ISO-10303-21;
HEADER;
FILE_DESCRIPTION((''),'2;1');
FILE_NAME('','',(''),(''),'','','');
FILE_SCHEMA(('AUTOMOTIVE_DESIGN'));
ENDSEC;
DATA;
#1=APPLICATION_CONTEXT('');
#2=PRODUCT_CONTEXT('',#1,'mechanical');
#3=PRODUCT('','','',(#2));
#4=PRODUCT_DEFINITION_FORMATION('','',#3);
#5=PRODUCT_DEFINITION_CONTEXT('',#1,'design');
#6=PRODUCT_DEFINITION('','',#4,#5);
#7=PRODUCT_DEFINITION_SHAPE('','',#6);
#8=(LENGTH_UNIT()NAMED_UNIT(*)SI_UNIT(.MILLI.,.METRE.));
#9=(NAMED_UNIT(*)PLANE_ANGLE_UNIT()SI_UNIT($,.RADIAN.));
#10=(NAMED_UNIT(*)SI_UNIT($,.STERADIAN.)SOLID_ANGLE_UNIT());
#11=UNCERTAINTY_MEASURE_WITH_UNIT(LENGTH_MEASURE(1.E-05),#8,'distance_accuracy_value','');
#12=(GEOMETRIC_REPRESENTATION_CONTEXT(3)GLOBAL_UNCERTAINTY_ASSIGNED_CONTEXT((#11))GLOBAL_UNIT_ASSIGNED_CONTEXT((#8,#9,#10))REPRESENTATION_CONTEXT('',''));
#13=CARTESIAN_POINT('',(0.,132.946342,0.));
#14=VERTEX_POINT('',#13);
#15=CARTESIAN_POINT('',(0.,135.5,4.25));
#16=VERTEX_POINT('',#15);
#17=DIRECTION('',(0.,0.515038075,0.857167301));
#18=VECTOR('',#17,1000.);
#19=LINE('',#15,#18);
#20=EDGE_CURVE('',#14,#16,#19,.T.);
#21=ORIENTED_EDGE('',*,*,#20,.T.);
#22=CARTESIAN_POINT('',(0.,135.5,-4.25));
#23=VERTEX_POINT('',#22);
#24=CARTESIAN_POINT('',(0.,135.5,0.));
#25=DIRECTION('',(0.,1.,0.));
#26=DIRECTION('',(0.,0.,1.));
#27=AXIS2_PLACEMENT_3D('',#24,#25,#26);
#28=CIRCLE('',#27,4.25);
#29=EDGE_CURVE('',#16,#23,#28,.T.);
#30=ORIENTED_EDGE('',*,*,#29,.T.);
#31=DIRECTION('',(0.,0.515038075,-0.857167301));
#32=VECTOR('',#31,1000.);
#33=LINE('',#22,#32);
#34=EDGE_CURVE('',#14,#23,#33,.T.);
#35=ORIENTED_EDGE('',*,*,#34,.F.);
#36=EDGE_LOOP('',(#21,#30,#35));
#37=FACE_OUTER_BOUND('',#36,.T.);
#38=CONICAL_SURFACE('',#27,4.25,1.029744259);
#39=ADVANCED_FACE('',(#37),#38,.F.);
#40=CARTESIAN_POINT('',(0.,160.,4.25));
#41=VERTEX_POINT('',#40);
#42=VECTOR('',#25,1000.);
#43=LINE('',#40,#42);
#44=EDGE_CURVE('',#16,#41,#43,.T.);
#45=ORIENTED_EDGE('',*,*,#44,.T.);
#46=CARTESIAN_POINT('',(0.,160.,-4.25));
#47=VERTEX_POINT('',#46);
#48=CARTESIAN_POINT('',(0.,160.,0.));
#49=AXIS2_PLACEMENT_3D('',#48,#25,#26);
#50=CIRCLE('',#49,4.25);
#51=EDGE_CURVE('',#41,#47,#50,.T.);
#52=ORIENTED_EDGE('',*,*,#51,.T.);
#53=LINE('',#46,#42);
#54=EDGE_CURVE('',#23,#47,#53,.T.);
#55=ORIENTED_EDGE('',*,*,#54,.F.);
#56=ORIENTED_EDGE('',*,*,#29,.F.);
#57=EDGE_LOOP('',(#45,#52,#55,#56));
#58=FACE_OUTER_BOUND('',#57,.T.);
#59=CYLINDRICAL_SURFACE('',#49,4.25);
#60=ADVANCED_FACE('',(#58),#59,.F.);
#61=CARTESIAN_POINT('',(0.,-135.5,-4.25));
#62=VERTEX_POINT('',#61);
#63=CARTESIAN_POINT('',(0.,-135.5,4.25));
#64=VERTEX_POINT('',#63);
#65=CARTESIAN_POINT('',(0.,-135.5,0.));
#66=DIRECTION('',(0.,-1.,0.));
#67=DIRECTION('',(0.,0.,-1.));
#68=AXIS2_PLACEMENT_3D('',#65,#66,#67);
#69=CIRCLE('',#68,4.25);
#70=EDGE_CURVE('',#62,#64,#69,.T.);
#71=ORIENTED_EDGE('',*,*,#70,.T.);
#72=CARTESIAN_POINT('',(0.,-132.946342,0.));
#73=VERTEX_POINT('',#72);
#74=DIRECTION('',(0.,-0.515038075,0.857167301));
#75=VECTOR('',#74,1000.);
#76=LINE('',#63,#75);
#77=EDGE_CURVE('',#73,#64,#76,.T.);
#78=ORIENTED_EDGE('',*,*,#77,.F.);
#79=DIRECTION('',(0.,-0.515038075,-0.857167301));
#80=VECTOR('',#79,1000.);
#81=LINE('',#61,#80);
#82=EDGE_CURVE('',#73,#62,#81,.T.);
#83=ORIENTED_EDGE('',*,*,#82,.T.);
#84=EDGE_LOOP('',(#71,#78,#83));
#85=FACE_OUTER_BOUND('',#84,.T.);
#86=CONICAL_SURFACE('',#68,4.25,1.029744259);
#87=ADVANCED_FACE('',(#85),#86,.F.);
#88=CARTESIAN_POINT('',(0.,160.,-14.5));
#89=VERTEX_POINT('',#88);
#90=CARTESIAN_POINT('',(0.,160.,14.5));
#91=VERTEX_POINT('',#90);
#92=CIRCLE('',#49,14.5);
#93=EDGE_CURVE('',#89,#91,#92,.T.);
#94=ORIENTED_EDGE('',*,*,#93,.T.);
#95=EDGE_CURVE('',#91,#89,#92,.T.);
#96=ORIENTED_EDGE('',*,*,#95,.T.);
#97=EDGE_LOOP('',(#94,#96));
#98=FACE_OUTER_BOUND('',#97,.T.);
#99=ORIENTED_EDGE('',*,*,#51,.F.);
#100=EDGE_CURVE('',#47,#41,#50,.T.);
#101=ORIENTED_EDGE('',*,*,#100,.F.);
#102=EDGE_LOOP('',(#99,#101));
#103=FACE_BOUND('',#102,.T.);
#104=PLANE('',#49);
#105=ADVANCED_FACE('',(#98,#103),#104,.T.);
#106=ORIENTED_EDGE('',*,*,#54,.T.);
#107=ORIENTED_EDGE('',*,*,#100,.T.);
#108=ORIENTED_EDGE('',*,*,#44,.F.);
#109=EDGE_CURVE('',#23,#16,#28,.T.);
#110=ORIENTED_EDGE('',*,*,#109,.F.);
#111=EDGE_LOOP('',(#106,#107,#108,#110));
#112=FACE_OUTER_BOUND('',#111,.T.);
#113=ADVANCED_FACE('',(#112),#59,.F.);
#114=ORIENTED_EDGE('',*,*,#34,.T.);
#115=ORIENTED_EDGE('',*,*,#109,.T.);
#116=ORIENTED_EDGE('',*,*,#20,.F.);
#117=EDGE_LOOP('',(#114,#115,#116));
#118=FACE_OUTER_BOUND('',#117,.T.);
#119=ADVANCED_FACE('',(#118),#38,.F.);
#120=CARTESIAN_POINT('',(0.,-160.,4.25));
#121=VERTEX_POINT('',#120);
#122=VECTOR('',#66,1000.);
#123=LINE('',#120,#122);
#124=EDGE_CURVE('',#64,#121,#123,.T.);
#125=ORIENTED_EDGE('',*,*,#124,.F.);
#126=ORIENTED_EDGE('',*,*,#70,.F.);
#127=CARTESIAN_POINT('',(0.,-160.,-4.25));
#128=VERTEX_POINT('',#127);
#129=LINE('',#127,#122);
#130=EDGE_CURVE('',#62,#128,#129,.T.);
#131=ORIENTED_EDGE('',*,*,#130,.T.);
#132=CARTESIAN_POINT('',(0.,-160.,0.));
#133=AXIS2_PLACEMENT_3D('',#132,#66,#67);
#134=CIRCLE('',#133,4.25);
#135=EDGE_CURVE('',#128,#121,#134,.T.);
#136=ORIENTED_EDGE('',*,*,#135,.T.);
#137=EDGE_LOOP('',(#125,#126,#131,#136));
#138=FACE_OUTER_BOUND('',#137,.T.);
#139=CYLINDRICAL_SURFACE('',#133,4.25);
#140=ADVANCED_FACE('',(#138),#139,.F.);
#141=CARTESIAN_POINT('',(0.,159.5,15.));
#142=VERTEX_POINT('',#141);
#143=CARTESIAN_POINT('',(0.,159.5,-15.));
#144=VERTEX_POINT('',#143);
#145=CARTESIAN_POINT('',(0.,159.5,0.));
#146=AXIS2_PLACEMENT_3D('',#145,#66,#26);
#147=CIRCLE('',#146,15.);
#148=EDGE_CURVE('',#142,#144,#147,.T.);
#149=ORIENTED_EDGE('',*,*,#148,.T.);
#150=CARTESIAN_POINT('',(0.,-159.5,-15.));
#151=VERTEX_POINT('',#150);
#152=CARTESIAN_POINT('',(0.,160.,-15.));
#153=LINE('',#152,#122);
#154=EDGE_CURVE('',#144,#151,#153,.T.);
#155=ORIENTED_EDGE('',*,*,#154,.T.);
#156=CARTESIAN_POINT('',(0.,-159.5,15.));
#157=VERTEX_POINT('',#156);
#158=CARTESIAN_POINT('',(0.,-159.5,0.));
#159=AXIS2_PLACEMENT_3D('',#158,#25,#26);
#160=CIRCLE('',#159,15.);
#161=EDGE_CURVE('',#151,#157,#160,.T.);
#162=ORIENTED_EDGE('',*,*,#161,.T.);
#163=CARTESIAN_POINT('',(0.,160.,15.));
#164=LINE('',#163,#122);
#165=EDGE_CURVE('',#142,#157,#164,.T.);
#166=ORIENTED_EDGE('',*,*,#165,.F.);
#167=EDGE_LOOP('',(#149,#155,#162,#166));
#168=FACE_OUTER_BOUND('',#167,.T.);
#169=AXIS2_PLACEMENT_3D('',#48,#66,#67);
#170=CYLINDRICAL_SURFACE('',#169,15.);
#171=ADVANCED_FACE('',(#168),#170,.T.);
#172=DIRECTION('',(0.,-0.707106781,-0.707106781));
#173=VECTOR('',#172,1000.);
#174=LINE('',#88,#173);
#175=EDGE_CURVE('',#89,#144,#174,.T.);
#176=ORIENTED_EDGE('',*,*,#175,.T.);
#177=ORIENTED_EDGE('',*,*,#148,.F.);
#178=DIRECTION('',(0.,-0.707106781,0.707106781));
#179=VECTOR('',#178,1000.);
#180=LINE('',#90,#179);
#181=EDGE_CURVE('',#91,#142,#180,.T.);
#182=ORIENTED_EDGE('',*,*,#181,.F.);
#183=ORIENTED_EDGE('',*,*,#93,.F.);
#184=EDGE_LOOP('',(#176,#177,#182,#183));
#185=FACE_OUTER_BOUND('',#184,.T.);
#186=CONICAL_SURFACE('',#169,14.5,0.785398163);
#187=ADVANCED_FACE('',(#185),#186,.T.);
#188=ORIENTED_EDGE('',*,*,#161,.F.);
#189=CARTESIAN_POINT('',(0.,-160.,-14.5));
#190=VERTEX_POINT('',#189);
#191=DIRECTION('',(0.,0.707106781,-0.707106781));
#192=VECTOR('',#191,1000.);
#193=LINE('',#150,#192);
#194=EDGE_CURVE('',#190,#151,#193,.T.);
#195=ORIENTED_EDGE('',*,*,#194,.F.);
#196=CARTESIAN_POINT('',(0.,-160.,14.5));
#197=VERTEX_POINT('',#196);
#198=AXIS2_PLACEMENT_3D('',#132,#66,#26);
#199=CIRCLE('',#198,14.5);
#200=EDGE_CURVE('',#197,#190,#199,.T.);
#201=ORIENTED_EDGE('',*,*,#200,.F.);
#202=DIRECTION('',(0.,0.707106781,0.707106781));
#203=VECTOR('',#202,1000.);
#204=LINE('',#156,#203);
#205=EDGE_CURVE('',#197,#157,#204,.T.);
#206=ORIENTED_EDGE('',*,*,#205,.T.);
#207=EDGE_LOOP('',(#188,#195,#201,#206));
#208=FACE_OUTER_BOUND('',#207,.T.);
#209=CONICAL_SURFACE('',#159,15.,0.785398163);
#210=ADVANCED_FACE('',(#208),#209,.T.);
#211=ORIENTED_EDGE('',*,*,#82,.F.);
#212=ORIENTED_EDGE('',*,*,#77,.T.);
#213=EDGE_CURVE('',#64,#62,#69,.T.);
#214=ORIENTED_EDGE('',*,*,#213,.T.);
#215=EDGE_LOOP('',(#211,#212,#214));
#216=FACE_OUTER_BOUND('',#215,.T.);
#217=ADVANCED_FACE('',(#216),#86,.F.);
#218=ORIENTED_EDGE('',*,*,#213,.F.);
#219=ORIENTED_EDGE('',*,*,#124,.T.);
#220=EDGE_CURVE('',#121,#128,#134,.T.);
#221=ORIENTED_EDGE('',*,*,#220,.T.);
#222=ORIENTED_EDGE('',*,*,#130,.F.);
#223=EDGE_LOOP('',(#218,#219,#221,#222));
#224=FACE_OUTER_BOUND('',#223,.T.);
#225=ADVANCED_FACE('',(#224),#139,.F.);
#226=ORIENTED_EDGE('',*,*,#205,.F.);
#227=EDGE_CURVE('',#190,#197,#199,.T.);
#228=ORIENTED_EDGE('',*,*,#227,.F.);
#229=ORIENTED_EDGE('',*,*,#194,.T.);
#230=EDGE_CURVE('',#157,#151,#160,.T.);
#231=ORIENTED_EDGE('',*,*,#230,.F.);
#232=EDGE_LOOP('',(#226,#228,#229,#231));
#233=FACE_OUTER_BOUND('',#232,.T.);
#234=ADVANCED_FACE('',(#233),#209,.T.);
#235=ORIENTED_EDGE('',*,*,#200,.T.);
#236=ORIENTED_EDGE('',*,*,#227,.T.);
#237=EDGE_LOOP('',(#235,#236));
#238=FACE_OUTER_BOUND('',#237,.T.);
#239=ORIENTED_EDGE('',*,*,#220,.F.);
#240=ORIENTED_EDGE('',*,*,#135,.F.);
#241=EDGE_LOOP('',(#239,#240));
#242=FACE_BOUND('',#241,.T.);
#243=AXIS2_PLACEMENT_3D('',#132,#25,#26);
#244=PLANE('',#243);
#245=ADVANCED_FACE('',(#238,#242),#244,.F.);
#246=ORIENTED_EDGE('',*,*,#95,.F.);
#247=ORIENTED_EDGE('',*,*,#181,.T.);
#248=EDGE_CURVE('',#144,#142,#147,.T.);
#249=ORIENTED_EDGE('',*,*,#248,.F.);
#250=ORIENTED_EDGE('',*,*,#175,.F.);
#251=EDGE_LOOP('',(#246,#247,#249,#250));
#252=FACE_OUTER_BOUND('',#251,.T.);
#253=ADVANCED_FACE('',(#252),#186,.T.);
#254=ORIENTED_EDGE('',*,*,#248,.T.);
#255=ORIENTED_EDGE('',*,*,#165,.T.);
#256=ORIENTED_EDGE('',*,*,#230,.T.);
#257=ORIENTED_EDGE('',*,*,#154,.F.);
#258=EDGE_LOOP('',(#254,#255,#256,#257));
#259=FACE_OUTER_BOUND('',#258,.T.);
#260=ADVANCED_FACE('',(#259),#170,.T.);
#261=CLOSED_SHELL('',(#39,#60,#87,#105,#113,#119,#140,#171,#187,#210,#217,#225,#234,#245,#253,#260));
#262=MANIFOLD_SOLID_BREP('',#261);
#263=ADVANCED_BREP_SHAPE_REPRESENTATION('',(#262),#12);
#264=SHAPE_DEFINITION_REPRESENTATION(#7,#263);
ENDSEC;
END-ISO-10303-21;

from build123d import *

# Parameters (mm, degrees)
SKETCH_1_R              = 15
EXTRUDE_1_DEPTH         = 160
CHAMFER_1_SIZE          = 0.5
HOLE_WIZARD_M10_2_D     = 8.5
HOLE_WIZARD_M10_2_DEPTH = 24.5
HOLE_WIZARD_M10_2_TIP   = 2.553657631
HOLE_WIZARD_M10_1_D     = 8.5
HOLE_WIZARD_M10_1_DEPTH = 24.5
HOLE_WIZARD_M10_1_TIP   = 2.553657631


with BuildPart() as part:
    # 草图1 → 凸台-拉伸1 (new, symmetric)
    with BuildSketch(Plane(origin=(0, 0, 0), x_dir=(1, 0, 0), z_dir=(0, 1, 0))):
        with Locations(Location((0, 0, 0), (0, 0, 270))):
            Circle(SKETCH_1_R)
    extrude(amount=EXTRUDE_1_DEPTH, both=True)

    # 倒角1
    chamfer_1_edges = [part.edges().sort_by_distance(p)[0] for p in [
        (0, -160, -15),
        (0, 160, -15),
    ]]
    chamfer(chamfer_1_edges, length=CHAMFER_1_SIZE)

    # M10 螺纹孔2
    with Locations(Plane(origin=(0, 160, 0), x_dir=(1, 0, 0), z_dir=(0, 1, 0))):
        with Locations((0, 0)):
            Hole(HOLE_WIZARD_M10_2_D / 2, depth=HOLE_WIZARD_M10_2_DEPTH)
            with Locations((0, 0, -(HOLE_WIZARD_M10_2_DEPTH + HOLE_WIZARD_M10_2_TIP / 2))):  # 118° drill point
                Cone(0, HOLE_WIZARD_M10_2_D / 2, HOLE_WIZARD_M10_2_TIP, mode=Mode.SUBTRACT)

    # M10 螺纹孔1
    with Locations(Plane(origin=(0, -160, 0), x_dir=(-1, 0, 0), z_dir=(0, -1, 0))):
        with Locations((0, 0)):
            Hole(HOLE_WIZARD_M10_1_D / 2, depth=HOLE_WIZARD_M10_1_DEPTH)
            with Locations((0, 0, -(HOLE_WIZARD_M10_1_DEPTH + HOLE_WIZARD_M10_1_TIP / 2))):  # 118° drill point
                Cone(0, HOLE_WIZARD_M10_1_D / 2, HOLE_WIZARD_M10_1_TIP, mode=Mode.SUBTRACT)


solid = part.part
